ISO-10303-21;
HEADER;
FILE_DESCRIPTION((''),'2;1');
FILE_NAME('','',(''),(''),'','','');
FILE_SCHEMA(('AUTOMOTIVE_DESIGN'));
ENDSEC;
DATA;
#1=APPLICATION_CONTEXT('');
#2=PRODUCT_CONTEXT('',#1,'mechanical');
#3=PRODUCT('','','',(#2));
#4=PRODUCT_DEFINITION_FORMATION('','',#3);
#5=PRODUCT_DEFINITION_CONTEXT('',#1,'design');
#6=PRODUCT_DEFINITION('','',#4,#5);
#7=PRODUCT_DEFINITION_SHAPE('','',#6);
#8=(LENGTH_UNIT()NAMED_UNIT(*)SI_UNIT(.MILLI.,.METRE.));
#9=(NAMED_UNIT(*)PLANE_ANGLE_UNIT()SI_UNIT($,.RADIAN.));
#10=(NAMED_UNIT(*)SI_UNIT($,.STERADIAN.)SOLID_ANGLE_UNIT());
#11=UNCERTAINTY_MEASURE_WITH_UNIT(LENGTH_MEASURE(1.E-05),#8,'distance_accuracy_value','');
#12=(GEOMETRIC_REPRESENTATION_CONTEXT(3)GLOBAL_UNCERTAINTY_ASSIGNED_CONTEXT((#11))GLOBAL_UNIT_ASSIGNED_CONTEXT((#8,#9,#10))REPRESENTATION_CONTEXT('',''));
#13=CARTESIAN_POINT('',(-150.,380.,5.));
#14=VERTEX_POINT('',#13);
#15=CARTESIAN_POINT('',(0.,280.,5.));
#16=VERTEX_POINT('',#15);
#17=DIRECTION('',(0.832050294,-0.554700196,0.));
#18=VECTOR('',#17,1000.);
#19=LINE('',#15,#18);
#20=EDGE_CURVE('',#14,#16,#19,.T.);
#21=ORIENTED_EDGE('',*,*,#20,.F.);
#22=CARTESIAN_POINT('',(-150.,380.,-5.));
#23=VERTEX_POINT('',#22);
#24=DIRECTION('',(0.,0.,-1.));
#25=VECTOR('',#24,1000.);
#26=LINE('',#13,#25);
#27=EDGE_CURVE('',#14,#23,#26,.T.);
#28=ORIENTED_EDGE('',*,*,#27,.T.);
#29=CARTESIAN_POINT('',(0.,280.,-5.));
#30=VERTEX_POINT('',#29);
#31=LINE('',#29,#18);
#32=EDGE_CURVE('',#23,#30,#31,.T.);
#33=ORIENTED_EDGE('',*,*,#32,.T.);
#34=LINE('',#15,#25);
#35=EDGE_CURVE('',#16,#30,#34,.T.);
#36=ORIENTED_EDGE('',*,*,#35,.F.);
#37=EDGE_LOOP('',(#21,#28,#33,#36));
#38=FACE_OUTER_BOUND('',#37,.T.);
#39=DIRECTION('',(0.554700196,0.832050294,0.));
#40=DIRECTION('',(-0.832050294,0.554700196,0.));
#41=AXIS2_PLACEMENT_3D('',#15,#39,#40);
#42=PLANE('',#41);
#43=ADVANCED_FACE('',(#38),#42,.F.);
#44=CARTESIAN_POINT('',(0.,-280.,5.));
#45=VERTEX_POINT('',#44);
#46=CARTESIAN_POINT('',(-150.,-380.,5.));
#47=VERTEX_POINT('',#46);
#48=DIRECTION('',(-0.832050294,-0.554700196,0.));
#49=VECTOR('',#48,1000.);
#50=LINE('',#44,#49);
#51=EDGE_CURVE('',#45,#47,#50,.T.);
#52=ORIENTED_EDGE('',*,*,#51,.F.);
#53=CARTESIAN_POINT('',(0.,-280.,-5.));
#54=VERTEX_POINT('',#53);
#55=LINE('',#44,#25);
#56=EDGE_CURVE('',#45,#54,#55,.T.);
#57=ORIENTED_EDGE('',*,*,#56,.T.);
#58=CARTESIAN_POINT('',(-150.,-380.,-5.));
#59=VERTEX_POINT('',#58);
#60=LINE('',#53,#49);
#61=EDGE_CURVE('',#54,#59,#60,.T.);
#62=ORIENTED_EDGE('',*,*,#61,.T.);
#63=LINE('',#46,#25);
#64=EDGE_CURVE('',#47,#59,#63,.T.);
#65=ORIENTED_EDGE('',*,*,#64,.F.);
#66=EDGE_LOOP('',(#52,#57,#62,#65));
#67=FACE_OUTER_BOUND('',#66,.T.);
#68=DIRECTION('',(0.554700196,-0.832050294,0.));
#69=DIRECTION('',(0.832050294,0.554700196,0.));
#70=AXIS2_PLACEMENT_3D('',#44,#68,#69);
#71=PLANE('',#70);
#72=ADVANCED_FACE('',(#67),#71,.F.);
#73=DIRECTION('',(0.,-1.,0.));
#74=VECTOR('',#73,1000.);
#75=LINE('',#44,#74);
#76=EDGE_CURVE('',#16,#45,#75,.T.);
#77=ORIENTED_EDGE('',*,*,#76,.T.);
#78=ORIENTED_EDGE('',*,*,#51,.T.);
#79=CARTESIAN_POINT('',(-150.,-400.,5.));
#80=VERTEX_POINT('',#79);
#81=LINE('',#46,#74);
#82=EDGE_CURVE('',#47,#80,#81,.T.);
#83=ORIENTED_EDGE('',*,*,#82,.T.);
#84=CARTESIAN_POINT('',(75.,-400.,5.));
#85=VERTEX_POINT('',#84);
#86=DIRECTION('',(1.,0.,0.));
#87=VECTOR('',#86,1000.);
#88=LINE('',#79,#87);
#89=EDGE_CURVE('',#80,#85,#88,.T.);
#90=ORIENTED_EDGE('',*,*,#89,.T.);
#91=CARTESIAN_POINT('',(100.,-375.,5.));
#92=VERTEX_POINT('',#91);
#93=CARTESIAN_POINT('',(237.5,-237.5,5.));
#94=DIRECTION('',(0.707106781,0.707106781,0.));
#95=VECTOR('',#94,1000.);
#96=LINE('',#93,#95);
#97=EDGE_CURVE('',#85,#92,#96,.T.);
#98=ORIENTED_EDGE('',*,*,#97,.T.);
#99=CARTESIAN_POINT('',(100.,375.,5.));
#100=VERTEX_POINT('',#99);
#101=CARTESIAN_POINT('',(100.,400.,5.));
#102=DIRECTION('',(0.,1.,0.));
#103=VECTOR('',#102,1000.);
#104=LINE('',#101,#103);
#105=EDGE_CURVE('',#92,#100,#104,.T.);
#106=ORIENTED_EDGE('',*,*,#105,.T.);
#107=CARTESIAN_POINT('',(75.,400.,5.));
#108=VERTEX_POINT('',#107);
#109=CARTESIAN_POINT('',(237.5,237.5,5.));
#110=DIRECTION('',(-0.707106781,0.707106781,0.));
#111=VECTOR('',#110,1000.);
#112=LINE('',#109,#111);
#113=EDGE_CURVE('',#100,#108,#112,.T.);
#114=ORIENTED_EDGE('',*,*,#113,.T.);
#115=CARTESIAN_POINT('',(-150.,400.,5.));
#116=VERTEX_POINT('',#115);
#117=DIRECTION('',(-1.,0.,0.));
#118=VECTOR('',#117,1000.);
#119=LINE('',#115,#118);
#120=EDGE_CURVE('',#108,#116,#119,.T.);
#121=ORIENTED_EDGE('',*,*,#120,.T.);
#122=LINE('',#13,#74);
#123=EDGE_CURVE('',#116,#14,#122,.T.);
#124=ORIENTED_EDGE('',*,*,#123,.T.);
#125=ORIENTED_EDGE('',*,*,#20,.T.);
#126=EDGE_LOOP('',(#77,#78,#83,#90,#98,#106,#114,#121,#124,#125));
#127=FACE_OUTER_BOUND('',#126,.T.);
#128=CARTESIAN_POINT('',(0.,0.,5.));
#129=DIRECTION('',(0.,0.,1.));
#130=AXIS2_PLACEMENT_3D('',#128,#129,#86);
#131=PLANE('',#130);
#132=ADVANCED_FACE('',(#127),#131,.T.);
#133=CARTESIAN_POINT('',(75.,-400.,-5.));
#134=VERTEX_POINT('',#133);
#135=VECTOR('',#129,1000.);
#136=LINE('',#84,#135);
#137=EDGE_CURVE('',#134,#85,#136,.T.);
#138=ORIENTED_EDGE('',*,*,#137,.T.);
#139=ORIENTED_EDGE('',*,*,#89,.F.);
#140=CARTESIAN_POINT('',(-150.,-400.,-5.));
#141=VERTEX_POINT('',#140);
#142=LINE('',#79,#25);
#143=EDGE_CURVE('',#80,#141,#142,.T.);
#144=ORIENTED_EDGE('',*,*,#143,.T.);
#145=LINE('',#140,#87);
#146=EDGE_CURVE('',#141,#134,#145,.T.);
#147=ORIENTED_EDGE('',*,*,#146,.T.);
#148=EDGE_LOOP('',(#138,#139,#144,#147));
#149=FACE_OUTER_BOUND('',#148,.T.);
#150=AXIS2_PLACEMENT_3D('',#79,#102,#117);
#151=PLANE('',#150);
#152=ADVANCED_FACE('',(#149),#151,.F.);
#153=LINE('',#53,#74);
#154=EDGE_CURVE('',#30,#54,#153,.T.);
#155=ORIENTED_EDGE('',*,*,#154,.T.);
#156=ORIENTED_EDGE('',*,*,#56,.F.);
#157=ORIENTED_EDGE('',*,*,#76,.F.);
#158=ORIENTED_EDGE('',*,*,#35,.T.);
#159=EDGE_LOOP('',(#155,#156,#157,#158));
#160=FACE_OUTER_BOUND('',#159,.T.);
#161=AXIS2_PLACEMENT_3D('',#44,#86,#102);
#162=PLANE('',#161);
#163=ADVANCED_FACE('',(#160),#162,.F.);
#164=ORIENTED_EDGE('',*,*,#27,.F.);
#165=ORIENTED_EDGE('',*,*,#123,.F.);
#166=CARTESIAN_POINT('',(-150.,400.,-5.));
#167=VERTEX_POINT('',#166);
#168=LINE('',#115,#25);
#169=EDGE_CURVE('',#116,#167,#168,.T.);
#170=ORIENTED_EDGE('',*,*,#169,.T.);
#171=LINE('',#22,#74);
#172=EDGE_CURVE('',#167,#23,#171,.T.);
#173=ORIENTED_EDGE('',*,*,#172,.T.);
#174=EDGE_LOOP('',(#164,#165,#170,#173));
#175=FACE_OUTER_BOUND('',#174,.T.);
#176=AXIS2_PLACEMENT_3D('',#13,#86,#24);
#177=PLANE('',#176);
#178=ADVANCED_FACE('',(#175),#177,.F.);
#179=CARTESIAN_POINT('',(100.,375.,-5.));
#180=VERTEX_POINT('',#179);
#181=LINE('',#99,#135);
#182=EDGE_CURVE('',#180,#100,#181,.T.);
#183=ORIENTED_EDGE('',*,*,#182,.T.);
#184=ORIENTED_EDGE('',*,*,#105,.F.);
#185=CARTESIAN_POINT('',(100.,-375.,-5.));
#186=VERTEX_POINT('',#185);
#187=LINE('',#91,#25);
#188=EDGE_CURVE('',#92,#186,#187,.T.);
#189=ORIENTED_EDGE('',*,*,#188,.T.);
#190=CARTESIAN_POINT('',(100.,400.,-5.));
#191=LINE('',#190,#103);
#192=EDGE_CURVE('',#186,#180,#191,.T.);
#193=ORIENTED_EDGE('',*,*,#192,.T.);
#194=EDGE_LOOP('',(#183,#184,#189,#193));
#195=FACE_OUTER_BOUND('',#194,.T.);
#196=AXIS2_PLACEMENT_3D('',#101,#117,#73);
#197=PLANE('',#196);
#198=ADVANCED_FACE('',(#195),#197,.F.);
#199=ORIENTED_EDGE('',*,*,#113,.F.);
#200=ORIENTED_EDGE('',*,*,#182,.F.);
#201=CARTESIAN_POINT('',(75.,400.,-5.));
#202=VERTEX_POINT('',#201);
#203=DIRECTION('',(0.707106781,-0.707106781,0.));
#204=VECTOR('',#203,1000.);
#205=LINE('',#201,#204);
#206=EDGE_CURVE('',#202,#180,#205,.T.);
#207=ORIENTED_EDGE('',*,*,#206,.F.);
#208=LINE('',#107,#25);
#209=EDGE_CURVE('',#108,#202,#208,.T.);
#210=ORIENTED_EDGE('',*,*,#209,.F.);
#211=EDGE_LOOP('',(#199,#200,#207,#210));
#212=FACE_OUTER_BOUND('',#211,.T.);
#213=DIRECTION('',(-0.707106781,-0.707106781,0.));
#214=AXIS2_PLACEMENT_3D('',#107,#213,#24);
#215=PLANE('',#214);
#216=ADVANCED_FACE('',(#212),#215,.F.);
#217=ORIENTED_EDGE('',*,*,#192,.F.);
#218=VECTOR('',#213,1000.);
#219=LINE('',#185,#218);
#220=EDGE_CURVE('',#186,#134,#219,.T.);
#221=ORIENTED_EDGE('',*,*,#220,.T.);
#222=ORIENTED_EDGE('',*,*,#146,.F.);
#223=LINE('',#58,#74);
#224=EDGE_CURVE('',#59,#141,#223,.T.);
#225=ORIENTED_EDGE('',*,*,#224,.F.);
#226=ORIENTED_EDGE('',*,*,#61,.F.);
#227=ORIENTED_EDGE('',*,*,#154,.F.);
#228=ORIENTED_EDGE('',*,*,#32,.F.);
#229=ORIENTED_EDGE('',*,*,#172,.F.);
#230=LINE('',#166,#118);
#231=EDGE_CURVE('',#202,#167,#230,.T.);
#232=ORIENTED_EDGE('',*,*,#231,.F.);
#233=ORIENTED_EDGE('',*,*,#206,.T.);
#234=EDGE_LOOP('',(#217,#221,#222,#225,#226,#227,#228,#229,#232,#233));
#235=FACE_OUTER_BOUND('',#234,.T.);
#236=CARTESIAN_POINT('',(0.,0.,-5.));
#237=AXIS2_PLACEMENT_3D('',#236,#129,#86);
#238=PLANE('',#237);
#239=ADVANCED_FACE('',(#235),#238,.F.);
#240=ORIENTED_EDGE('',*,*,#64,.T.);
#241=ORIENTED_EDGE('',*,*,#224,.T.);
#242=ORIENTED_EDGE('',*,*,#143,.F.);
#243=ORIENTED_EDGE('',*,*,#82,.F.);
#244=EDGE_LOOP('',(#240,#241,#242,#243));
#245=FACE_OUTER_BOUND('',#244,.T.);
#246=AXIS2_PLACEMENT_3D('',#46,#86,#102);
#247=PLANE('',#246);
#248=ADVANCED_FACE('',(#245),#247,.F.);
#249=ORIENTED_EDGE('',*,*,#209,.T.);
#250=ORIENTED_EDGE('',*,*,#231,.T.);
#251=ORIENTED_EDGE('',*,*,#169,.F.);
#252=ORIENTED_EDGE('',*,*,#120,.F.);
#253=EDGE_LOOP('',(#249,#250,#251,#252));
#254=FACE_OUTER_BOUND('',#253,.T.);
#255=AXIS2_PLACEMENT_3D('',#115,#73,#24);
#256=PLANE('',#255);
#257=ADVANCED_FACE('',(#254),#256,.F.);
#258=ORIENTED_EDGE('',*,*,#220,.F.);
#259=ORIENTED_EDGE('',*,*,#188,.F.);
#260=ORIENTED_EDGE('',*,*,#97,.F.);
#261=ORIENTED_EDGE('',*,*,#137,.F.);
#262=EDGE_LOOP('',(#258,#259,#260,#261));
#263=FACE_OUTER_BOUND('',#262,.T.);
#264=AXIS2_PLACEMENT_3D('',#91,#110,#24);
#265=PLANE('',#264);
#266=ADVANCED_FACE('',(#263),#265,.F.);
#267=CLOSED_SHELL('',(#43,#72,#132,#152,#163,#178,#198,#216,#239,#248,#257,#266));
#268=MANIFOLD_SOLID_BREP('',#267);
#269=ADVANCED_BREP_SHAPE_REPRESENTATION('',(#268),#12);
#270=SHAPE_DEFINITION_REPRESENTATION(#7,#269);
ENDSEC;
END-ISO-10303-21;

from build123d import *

# Parameters (mm, degrees)
BOSS_EXTRUDE1_DEPTH = 5
CHAMFER1_SIZE       = 25


with BuildPart() as part:
    # Sketch1 → Boss-Extrude1 (new, symmetric)
    with BuildSketch(Plane.XY):
        Polygon((0, -280), (0, 280), (-150, 380), (-150, 400), (100, 400), (100, -400), (-150, -400), (-150, -380), align=None)
    extrude(amount=BOSS_EXTRUDE1_DEPTH, both=True)

    # Chamfer1
    chamfer1_edges = [part.edges().sort_by_distance(p)[0] for p in [
        (100, 400, 0),
        (100, -400, 0),
    ]]
    chamfer(chamfer1_edges, length=CHAMFER1_SIZE)


solid = part.part
